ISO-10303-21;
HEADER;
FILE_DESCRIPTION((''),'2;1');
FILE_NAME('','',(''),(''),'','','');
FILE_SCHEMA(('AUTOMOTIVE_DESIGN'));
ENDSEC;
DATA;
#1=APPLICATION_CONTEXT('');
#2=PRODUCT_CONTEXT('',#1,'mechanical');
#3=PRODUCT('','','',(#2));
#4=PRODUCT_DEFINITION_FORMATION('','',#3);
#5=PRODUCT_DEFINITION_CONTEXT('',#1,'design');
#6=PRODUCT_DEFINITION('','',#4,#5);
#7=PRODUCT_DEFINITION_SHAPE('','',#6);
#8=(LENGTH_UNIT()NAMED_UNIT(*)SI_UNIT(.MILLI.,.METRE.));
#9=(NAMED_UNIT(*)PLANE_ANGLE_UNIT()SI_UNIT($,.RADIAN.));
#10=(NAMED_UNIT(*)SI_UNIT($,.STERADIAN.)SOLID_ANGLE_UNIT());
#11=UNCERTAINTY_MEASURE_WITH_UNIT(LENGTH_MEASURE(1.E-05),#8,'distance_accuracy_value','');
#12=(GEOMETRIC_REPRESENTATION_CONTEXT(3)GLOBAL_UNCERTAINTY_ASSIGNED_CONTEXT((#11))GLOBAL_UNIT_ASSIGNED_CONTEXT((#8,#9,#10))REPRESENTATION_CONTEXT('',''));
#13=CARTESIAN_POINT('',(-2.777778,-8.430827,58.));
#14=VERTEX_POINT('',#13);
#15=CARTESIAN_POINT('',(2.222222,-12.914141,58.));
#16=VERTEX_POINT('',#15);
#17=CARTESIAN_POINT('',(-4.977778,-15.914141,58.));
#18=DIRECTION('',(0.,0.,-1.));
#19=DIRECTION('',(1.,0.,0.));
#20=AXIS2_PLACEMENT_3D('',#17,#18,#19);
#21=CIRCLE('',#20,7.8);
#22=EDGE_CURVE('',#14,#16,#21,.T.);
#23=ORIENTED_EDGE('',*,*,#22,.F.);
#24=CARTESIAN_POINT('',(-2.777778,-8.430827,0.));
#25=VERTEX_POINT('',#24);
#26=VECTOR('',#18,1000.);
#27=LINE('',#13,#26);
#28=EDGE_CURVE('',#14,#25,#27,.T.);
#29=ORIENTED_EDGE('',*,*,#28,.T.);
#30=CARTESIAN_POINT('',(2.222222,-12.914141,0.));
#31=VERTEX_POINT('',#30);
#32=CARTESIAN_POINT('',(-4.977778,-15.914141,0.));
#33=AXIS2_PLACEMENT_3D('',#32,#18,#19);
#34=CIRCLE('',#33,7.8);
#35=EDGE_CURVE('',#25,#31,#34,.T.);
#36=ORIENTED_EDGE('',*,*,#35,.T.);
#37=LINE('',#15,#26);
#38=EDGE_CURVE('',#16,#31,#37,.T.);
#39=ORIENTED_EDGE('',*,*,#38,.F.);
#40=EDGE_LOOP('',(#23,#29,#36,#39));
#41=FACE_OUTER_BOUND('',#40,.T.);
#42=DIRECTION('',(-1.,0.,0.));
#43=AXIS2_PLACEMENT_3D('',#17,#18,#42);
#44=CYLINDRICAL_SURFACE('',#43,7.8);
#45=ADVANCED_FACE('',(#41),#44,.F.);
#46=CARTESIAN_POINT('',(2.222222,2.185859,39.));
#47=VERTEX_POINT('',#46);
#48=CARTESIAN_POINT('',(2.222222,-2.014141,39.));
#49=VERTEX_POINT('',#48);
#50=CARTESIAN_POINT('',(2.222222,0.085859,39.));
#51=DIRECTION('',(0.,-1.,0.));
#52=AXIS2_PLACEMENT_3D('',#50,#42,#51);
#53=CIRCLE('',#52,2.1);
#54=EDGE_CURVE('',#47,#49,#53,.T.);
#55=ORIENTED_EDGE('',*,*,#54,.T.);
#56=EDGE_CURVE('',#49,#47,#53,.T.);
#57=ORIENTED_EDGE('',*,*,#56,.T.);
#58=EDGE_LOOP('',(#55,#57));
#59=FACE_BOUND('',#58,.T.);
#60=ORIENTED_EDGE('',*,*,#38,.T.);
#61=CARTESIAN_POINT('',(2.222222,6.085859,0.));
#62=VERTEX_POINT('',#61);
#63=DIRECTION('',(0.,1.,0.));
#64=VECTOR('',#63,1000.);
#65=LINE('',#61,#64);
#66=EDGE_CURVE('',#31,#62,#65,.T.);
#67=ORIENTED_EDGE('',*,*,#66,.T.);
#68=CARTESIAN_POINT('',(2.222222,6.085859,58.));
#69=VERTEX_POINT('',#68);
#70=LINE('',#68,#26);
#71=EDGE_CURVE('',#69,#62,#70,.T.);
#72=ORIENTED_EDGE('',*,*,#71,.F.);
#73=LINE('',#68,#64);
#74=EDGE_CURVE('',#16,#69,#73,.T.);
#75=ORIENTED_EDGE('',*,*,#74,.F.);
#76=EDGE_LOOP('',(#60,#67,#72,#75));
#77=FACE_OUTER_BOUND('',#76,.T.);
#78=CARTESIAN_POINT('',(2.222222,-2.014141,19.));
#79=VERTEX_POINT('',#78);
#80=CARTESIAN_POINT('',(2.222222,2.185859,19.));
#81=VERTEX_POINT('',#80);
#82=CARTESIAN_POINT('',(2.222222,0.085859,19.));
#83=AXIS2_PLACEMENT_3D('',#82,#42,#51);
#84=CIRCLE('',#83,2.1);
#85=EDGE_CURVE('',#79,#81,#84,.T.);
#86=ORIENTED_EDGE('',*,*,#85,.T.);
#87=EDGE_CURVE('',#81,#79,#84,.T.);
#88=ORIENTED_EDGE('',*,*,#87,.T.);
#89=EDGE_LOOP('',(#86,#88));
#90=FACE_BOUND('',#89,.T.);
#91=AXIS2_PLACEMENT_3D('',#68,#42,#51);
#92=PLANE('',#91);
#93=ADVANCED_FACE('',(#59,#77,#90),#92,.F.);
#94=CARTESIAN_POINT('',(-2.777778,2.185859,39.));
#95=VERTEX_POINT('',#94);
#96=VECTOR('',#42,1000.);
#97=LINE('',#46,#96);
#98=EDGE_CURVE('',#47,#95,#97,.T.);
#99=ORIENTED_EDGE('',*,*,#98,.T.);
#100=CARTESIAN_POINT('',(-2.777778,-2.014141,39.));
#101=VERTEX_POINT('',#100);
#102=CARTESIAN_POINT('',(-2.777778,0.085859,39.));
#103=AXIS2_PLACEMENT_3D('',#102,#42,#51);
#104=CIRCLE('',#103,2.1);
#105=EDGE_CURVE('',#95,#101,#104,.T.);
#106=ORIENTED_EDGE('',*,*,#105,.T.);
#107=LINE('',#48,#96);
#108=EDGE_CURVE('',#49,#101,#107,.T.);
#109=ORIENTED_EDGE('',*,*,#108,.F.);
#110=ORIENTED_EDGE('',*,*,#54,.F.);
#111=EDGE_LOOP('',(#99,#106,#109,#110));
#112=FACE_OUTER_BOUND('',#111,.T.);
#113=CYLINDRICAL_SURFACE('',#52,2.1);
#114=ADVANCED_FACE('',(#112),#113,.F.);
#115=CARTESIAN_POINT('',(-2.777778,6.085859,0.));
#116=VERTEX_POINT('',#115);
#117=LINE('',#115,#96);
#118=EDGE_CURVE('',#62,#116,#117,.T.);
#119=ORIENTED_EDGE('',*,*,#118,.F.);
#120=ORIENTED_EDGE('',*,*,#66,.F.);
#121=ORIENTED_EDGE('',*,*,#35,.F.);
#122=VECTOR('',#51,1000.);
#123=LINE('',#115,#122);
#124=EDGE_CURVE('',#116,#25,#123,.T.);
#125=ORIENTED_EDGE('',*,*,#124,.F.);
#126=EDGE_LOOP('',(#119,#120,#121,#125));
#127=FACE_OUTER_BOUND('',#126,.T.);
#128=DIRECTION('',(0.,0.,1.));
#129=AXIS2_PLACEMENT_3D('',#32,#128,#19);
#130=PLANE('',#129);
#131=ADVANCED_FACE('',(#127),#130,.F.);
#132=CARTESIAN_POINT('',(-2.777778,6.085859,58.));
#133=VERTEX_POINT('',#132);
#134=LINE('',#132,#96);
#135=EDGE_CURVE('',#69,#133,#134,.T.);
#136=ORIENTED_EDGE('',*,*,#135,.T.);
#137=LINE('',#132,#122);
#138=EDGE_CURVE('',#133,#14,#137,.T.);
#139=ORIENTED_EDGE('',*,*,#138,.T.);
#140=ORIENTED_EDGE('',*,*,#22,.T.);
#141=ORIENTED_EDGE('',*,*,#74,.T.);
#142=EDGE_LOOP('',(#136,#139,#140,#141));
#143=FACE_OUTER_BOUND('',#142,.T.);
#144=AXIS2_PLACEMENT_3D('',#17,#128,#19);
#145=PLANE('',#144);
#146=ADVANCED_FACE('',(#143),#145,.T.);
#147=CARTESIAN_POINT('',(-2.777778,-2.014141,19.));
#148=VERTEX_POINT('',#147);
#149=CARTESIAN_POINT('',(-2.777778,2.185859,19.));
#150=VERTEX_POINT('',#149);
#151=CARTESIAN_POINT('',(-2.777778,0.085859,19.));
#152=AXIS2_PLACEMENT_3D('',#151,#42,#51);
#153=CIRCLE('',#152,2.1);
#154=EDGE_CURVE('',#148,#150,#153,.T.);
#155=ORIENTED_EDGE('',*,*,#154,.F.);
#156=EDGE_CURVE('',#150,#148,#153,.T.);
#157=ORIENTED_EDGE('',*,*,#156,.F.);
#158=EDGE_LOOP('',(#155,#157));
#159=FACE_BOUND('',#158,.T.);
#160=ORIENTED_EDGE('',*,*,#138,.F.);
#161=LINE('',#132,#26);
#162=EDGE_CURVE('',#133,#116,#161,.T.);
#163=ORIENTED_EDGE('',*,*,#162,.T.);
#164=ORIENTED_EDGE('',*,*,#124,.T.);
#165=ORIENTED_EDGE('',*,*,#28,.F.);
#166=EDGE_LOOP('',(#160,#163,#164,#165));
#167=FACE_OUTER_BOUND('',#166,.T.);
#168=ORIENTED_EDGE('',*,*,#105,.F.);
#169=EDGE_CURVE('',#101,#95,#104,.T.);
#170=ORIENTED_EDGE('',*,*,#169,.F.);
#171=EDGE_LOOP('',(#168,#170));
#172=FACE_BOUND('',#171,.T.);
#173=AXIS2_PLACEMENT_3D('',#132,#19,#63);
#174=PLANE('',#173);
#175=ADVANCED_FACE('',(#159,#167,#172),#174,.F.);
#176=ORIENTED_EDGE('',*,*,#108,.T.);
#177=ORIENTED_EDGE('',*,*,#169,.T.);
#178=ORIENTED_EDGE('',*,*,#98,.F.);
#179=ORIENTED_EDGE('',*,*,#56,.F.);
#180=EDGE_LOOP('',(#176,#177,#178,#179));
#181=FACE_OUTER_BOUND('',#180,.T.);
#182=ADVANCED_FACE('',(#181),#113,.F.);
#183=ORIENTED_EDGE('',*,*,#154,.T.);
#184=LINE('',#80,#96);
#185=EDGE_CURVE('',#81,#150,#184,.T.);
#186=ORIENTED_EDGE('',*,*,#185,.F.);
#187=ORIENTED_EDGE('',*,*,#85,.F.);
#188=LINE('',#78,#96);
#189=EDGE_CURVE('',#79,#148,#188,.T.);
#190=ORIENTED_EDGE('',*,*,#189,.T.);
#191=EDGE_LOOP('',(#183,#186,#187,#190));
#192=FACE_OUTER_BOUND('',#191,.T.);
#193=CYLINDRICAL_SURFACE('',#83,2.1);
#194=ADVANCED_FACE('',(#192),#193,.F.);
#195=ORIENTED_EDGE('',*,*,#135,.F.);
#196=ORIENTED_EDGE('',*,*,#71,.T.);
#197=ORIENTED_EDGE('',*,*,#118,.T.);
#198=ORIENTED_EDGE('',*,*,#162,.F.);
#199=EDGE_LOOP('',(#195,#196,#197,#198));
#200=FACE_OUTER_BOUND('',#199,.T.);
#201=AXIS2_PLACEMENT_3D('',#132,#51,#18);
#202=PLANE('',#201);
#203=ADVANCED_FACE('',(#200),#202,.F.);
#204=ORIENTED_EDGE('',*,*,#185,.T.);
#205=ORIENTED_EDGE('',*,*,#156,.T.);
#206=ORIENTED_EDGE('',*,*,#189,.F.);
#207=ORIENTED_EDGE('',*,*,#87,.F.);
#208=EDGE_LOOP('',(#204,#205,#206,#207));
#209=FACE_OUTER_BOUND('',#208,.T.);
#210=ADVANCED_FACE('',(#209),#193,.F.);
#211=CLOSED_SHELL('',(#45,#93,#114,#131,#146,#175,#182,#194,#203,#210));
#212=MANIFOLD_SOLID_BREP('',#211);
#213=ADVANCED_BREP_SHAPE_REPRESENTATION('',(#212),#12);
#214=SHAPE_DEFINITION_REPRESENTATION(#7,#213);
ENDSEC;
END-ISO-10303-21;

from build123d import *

# Parameters (mm, degrees)
EXTRUDE_1_DEPTH     = 58
SKETCH_2_R          = 2.1
CUT_EXTRUDE_1_DEPTH = 60.630319876


with BuildPart() as part:
    # 草图1 → 凸台-拉伸1 (new body)
    with BuildSketch(Plane.XY):
        with BuildLine():
            Line((-2.777777778, 6.085858586), (2.222222222, 6.085858586))
            Line((2.222222222, 6.085858586), (2.222222222, -12.914141414))
            ThreePointArc((2.222222222, -12.914141414), (0.22943144, -10.106820848), (-2.777777778, -8.430826641))
            Line((-2.777777778, -8.430826641), (-2.777777778, 6.085858586))
        make_face()
    extrude(amount=EXTRUDE_1_DEPTH)

    # 草图2 → 切除-拉伸1 (cut, through all)
    with BuildSketch(Plane.ZY.offset(2.777777778)):
        with Locations(Location((19, 0.085858586, 0), (0, 0, 270))):
            Circle(SKETCH_2_R)
        with Locations(Location((39, 0.085858586, 0), (0, 0, 270))):
            Circle(SKETCH_2_R)
    extrude(amount=-CUT_EXTRUDE_1_DEPTH, mode=Mode.SUBTRACT)


solid = part.part
